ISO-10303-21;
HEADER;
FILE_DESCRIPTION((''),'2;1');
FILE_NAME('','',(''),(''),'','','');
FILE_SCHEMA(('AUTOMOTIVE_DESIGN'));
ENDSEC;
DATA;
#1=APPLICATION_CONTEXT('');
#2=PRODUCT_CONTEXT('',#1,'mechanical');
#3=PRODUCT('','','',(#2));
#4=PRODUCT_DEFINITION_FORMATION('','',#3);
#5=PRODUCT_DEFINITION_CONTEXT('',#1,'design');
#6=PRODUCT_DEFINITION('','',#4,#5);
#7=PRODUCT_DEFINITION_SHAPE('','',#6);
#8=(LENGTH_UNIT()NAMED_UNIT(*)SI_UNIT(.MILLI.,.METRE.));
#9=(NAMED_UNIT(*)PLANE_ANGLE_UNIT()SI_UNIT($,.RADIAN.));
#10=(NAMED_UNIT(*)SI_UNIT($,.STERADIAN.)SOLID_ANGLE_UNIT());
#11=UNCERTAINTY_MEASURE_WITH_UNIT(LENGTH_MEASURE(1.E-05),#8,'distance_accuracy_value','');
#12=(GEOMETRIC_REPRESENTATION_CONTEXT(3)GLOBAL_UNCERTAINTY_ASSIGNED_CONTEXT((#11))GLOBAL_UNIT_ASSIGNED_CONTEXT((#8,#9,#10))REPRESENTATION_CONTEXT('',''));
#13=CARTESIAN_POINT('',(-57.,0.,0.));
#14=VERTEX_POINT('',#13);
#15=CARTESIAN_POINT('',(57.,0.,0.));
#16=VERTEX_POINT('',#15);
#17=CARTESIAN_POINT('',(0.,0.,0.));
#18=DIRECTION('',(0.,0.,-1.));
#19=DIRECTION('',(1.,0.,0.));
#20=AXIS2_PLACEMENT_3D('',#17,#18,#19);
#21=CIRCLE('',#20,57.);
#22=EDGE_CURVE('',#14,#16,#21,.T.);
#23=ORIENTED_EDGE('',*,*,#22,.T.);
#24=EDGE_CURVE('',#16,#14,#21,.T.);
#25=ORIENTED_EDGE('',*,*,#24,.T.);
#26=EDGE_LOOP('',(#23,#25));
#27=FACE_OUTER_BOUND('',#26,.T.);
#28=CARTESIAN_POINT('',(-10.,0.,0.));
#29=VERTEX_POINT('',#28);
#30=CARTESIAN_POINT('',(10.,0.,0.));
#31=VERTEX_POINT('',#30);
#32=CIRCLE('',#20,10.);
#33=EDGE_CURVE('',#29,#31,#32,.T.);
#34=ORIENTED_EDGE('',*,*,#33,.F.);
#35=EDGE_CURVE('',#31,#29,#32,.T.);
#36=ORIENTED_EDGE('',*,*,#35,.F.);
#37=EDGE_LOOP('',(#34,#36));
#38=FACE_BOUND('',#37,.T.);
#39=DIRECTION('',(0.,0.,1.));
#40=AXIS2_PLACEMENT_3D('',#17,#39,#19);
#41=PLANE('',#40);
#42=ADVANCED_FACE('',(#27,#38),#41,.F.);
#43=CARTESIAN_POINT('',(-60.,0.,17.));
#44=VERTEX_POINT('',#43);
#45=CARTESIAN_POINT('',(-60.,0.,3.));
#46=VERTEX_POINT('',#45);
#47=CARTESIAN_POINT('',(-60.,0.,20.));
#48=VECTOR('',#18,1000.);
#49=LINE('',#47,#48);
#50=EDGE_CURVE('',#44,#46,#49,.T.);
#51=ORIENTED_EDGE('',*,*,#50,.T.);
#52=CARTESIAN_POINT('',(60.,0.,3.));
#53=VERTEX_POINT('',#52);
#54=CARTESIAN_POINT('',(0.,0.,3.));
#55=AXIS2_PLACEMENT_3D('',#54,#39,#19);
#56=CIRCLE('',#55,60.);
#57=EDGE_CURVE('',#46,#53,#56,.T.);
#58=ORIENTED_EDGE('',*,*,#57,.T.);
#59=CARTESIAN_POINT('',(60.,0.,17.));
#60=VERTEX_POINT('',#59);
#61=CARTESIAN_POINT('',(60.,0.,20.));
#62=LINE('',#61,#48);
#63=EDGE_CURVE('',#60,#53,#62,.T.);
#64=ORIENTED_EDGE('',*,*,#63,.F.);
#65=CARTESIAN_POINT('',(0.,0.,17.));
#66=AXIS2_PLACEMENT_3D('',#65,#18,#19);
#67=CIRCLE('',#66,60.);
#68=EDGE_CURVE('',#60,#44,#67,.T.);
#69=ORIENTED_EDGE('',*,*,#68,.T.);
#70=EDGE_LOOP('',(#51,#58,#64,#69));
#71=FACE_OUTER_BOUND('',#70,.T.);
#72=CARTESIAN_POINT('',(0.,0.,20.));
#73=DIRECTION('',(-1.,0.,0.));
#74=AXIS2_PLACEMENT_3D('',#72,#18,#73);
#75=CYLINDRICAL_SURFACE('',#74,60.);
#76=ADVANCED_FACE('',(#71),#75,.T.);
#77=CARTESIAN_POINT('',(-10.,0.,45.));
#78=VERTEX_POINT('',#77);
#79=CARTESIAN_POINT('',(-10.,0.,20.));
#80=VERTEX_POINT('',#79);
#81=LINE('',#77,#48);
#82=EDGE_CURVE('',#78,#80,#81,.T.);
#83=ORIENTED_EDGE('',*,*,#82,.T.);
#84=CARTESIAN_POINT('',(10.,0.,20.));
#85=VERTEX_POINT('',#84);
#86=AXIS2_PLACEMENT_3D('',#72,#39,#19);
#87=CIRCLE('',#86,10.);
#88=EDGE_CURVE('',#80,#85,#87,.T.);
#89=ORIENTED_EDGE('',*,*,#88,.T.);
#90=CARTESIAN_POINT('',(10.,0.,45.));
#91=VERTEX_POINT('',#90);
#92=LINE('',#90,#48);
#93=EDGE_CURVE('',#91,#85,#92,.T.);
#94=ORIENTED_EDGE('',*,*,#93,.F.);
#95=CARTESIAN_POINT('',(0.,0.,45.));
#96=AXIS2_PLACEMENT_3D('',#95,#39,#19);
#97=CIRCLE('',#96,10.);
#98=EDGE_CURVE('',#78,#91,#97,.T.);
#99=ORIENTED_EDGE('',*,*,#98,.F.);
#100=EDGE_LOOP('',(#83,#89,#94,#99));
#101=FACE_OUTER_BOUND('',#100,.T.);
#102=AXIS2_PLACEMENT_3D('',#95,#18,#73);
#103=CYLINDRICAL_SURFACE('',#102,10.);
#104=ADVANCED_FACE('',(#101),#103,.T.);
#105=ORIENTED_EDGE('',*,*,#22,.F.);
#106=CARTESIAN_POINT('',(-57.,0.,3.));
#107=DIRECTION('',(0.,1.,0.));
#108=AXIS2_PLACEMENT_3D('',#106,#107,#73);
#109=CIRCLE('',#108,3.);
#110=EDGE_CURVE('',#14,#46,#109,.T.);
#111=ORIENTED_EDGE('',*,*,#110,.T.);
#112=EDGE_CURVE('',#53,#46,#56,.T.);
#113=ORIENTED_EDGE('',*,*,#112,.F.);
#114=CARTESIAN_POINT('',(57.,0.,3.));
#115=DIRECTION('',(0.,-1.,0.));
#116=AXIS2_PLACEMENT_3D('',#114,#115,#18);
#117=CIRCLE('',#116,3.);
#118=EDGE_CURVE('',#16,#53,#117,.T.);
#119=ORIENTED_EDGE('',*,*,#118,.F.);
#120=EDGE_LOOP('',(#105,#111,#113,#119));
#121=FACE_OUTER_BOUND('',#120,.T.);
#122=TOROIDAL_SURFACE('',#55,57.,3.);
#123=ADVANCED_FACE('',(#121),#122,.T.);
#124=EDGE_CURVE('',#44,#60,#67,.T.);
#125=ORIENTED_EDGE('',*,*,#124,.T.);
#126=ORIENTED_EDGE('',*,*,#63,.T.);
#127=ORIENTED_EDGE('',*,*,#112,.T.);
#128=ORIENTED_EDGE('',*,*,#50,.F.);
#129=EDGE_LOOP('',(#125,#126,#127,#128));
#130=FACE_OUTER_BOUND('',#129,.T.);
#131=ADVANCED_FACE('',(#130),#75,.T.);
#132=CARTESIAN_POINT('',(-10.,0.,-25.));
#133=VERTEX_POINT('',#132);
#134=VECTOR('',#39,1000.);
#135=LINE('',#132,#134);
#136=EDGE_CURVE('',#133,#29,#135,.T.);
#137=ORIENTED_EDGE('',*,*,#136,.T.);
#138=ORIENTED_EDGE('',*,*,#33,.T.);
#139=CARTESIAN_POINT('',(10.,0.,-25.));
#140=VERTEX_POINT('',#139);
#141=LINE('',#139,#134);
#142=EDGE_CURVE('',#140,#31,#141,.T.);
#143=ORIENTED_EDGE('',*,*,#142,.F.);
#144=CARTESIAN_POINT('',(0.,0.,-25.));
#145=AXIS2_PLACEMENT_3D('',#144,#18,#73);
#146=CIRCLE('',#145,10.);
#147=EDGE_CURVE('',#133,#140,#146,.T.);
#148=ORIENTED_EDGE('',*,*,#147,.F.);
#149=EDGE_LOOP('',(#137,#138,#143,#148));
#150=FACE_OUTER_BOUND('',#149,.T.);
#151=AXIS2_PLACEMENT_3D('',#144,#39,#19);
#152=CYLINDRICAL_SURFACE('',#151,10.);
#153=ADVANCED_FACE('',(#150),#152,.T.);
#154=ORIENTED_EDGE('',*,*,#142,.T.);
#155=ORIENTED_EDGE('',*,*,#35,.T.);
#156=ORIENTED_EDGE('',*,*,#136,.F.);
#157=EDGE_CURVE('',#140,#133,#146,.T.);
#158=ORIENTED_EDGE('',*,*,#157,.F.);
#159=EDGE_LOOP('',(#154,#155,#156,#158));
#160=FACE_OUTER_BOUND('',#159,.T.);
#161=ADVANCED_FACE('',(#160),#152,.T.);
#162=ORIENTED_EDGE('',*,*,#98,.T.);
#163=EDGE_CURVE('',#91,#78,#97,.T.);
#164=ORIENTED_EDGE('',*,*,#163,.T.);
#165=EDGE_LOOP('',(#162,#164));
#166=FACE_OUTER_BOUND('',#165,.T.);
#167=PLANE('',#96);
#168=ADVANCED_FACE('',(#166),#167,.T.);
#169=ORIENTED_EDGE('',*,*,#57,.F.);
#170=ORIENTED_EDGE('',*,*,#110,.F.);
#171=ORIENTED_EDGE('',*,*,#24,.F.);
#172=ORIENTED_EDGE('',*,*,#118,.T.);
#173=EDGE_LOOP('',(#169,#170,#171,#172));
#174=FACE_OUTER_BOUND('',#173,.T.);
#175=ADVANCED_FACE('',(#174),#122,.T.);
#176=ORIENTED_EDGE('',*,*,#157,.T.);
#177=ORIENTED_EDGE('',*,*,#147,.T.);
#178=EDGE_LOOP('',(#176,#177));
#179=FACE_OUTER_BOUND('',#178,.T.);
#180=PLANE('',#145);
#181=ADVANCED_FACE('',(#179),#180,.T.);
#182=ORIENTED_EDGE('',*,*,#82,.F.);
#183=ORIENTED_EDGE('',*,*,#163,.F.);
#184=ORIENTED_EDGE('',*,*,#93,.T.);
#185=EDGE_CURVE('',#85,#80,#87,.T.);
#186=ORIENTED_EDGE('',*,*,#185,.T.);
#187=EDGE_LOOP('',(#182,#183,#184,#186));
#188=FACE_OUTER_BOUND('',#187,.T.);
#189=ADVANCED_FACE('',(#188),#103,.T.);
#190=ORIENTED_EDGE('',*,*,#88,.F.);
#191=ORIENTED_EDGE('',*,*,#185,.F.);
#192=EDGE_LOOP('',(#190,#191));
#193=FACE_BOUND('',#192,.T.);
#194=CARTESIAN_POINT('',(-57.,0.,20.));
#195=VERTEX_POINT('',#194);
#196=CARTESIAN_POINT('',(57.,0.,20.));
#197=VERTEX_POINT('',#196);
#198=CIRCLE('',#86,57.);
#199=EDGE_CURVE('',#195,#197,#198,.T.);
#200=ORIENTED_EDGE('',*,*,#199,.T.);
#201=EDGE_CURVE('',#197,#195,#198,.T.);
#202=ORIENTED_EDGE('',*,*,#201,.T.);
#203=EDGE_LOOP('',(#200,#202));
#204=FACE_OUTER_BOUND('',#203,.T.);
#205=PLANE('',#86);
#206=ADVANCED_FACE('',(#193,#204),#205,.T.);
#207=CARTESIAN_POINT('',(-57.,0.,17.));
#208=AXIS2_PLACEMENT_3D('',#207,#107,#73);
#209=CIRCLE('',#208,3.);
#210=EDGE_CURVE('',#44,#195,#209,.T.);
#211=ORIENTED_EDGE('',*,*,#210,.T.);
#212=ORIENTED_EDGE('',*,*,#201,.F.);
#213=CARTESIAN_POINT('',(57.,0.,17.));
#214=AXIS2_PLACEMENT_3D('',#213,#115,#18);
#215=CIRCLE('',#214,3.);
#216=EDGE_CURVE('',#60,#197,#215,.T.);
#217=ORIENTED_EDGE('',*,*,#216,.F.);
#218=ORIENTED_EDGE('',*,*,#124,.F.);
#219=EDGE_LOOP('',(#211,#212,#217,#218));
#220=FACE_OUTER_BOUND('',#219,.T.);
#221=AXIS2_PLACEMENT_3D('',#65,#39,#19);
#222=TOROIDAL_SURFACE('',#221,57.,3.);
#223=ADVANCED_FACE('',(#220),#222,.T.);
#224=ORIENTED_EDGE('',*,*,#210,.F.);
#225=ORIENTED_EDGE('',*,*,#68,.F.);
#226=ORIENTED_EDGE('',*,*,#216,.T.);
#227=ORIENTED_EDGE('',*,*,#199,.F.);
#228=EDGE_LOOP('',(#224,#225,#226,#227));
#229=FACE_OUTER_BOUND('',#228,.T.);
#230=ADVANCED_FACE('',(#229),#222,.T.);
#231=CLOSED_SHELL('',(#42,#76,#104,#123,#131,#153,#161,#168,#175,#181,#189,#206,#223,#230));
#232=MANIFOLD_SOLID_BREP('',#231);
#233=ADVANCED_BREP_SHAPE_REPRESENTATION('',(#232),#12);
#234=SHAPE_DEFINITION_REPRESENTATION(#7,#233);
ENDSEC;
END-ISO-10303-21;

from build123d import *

# Parameters (mm, degrees)
SKETCH1_R           = 60
BOSS_EXTRUDE1_DEPTH = 20
FILLET1_R           = 3
SKETCH2_R           = 10
BOSS_EXTRUDE2_DEPTH = 25
BOSS_EXTRUDE3_START = 25
SKETCH3_R           = 10
BOSS_EXTRUDE3_DEPTH = 25


with BuildPart() as part:
    # Sketch1 → Boss-Extrude1 (new body)
    with BuildSketch(Plane.XY):
        Circle(SKETCH1_R)
    extrude(amount=BOSS_EXTRUDE1_DEPTH)

    # Fillet1
    fillet1_edges = [part.edges().sort_by_distance(p)[0] for p in [
        (-60, 0, 0),
        (-60, 0, 20),
    ]]
    fillet(fillet1_edges, radius=FILLET1_R)

    # Sketch2 → Boss-Extrude2 (add)
    with BuildSketch(Plane(origin=(0, 0, 0), x_dir=(-1, 0, 0), z_dir=(0, 0, -1))):
        with Locations(Location((0, 0, 0), (0, 0, 180))):
            Circle(SKETCH2_R)
    extrude(amount=BOSS_EXTRUDE2_DEPTH)

    # Sketch3 → Boss-Extrude3 (add)
    with BuildSketch(Plane.XY.offset(20).offset(BOSS_EXTRUDE3_START)):
        Circle(SKETCH3_R)
    extrude(amount=-BOSS_EXTRUDE3_DEPTH)


solid = part.part
